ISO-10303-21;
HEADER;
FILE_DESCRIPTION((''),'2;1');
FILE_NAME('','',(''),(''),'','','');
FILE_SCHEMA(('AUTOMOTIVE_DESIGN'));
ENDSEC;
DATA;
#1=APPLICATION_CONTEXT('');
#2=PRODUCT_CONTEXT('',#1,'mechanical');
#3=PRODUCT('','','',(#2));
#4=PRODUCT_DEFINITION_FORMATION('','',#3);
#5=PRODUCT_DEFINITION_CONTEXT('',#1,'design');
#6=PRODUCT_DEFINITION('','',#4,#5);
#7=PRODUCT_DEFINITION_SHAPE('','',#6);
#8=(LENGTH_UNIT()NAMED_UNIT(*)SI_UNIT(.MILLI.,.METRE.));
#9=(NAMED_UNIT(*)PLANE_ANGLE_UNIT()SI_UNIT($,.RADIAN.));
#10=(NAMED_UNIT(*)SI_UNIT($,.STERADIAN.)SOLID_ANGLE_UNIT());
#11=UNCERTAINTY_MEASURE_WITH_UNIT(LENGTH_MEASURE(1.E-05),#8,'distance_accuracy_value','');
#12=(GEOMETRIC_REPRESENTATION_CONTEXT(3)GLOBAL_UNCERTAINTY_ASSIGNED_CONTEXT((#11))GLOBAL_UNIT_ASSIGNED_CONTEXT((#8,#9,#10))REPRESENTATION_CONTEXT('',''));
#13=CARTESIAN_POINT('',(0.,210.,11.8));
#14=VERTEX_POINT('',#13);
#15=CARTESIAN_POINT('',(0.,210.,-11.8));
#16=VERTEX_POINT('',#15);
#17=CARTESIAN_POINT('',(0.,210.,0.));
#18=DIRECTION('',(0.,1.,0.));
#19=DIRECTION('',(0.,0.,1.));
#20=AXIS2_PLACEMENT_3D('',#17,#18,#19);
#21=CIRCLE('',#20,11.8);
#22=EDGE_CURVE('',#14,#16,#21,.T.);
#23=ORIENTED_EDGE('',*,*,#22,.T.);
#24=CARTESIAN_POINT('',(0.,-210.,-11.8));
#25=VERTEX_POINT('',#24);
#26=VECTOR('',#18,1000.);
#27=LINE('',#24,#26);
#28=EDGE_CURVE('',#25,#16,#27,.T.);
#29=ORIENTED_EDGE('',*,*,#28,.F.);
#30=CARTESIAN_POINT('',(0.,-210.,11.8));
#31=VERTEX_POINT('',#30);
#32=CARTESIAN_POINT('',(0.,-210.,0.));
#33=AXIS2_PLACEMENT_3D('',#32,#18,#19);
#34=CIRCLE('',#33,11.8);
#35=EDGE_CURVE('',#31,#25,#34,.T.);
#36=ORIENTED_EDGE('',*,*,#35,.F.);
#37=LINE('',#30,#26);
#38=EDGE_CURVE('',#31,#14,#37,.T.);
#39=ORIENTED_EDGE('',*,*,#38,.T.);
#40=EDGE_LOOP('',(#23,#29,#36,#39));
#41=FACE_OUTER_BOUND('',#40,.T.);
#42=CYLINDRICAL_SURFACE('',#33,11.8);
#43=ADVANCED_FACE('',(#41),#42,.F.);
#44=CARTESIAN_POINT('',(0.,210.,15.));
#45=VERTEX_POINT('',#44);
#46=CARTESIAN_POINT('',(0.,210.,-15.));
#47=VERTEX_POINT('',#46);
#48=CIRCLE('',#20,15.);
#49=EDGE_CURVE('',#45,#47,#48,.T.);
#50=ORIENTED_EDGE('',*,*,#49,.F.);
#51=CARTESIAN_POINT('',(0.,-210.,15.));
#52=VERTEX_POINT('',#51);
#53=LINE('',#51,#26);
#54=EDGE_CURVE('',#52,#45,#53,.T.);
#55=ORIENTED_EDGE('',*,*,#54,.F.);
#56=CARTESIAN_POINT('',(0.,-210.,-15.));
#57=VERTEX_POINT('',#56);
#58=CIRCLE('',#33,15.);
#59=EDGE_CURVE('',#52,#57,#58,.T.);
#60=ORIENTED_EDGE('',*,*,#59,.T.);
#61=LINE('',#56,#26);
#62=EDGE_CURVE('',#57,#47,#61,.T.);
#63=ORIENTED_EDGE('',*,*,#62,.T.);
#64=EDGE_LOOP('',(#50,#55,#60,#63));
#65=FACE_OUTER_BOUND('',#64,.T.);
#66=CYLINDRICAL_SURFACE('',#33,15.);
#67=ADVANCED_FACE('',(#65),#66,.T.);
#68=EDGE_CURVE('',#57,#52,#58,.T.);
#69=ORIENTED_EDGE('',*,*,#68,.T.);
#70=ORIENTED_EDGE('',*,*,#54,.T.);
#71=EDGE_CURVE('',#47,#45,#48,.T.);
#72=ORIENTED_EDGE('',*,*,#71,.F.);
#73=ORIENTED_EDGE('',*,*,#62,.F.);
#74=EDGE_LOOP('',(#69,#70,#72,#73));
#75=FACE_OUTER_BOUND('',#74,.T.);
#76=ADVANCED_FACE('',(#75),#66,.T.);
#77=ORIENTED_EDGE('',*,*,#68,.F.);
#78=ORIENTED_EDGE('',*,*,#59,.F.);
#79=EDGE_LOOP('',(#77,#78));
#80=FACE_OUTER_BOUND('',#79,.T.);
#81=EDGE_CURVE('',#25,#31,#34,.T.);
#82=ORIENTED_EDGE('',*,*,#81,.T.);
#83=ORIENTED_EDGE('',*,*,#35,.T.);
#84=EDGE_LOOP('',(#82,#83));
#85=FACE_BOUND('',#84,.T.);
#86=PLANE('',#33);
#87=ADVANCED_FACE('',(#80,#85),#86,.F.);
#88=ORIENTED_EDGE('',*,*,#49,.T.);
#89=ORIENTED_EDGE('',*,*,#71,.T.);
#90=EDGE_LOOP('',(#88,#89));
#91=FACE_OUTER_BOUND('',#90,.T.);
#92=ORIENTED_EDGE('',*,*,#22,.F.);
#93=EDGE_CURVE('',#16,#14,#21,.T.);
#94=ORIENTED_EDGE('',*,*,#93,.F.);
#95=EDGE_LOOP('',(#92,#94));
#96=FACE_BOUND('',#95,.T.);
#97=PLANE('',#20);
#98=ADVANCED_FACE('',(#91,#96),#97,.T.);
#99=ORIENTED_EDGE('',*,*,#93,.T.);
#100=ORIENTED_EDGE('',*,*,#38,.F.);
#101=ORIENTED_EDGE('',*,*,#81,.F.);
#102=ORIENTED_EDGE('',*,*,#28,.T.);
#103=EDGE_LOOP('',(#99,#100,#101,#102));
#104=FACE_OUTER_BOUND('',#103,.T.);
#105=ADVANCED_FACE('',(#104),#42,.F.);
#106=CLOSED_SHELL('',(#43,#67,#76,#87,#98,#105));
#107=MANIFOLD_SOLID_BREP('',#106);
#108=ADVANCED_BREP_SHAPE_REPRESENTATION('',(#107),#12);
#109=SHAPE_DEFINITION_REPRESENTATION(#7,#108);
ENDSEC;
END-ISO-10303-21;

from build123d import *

# Parameters (mm, degrees)
SKETCH1_R           = 15
SKETCH1_R_2         = 11.8
BOSS_EXTRUDE1_DEPTH = 210


with BuildPart() as part:
    # Sketch1 → Boss-Extrude1 (new, symmetric)
    with BuildSketch(Plane(origin=(0, 0, 0), x_dir=(1, 0, 0), z_dir=(0, 1, 0))):
        with Locations(Location((0, 0, 0), (0, 0, 270))):
            Circle(SKETCH1_R)
        with Locations(Location((0, 0, 0), (0, 0, 270))):
            Circle(SKETCH1_R_2, mode=Mode.SUBTRACT)
    extrude(amount=BOSS_EXTRUDE1_DEPTH, both=True)


solid = part.part
